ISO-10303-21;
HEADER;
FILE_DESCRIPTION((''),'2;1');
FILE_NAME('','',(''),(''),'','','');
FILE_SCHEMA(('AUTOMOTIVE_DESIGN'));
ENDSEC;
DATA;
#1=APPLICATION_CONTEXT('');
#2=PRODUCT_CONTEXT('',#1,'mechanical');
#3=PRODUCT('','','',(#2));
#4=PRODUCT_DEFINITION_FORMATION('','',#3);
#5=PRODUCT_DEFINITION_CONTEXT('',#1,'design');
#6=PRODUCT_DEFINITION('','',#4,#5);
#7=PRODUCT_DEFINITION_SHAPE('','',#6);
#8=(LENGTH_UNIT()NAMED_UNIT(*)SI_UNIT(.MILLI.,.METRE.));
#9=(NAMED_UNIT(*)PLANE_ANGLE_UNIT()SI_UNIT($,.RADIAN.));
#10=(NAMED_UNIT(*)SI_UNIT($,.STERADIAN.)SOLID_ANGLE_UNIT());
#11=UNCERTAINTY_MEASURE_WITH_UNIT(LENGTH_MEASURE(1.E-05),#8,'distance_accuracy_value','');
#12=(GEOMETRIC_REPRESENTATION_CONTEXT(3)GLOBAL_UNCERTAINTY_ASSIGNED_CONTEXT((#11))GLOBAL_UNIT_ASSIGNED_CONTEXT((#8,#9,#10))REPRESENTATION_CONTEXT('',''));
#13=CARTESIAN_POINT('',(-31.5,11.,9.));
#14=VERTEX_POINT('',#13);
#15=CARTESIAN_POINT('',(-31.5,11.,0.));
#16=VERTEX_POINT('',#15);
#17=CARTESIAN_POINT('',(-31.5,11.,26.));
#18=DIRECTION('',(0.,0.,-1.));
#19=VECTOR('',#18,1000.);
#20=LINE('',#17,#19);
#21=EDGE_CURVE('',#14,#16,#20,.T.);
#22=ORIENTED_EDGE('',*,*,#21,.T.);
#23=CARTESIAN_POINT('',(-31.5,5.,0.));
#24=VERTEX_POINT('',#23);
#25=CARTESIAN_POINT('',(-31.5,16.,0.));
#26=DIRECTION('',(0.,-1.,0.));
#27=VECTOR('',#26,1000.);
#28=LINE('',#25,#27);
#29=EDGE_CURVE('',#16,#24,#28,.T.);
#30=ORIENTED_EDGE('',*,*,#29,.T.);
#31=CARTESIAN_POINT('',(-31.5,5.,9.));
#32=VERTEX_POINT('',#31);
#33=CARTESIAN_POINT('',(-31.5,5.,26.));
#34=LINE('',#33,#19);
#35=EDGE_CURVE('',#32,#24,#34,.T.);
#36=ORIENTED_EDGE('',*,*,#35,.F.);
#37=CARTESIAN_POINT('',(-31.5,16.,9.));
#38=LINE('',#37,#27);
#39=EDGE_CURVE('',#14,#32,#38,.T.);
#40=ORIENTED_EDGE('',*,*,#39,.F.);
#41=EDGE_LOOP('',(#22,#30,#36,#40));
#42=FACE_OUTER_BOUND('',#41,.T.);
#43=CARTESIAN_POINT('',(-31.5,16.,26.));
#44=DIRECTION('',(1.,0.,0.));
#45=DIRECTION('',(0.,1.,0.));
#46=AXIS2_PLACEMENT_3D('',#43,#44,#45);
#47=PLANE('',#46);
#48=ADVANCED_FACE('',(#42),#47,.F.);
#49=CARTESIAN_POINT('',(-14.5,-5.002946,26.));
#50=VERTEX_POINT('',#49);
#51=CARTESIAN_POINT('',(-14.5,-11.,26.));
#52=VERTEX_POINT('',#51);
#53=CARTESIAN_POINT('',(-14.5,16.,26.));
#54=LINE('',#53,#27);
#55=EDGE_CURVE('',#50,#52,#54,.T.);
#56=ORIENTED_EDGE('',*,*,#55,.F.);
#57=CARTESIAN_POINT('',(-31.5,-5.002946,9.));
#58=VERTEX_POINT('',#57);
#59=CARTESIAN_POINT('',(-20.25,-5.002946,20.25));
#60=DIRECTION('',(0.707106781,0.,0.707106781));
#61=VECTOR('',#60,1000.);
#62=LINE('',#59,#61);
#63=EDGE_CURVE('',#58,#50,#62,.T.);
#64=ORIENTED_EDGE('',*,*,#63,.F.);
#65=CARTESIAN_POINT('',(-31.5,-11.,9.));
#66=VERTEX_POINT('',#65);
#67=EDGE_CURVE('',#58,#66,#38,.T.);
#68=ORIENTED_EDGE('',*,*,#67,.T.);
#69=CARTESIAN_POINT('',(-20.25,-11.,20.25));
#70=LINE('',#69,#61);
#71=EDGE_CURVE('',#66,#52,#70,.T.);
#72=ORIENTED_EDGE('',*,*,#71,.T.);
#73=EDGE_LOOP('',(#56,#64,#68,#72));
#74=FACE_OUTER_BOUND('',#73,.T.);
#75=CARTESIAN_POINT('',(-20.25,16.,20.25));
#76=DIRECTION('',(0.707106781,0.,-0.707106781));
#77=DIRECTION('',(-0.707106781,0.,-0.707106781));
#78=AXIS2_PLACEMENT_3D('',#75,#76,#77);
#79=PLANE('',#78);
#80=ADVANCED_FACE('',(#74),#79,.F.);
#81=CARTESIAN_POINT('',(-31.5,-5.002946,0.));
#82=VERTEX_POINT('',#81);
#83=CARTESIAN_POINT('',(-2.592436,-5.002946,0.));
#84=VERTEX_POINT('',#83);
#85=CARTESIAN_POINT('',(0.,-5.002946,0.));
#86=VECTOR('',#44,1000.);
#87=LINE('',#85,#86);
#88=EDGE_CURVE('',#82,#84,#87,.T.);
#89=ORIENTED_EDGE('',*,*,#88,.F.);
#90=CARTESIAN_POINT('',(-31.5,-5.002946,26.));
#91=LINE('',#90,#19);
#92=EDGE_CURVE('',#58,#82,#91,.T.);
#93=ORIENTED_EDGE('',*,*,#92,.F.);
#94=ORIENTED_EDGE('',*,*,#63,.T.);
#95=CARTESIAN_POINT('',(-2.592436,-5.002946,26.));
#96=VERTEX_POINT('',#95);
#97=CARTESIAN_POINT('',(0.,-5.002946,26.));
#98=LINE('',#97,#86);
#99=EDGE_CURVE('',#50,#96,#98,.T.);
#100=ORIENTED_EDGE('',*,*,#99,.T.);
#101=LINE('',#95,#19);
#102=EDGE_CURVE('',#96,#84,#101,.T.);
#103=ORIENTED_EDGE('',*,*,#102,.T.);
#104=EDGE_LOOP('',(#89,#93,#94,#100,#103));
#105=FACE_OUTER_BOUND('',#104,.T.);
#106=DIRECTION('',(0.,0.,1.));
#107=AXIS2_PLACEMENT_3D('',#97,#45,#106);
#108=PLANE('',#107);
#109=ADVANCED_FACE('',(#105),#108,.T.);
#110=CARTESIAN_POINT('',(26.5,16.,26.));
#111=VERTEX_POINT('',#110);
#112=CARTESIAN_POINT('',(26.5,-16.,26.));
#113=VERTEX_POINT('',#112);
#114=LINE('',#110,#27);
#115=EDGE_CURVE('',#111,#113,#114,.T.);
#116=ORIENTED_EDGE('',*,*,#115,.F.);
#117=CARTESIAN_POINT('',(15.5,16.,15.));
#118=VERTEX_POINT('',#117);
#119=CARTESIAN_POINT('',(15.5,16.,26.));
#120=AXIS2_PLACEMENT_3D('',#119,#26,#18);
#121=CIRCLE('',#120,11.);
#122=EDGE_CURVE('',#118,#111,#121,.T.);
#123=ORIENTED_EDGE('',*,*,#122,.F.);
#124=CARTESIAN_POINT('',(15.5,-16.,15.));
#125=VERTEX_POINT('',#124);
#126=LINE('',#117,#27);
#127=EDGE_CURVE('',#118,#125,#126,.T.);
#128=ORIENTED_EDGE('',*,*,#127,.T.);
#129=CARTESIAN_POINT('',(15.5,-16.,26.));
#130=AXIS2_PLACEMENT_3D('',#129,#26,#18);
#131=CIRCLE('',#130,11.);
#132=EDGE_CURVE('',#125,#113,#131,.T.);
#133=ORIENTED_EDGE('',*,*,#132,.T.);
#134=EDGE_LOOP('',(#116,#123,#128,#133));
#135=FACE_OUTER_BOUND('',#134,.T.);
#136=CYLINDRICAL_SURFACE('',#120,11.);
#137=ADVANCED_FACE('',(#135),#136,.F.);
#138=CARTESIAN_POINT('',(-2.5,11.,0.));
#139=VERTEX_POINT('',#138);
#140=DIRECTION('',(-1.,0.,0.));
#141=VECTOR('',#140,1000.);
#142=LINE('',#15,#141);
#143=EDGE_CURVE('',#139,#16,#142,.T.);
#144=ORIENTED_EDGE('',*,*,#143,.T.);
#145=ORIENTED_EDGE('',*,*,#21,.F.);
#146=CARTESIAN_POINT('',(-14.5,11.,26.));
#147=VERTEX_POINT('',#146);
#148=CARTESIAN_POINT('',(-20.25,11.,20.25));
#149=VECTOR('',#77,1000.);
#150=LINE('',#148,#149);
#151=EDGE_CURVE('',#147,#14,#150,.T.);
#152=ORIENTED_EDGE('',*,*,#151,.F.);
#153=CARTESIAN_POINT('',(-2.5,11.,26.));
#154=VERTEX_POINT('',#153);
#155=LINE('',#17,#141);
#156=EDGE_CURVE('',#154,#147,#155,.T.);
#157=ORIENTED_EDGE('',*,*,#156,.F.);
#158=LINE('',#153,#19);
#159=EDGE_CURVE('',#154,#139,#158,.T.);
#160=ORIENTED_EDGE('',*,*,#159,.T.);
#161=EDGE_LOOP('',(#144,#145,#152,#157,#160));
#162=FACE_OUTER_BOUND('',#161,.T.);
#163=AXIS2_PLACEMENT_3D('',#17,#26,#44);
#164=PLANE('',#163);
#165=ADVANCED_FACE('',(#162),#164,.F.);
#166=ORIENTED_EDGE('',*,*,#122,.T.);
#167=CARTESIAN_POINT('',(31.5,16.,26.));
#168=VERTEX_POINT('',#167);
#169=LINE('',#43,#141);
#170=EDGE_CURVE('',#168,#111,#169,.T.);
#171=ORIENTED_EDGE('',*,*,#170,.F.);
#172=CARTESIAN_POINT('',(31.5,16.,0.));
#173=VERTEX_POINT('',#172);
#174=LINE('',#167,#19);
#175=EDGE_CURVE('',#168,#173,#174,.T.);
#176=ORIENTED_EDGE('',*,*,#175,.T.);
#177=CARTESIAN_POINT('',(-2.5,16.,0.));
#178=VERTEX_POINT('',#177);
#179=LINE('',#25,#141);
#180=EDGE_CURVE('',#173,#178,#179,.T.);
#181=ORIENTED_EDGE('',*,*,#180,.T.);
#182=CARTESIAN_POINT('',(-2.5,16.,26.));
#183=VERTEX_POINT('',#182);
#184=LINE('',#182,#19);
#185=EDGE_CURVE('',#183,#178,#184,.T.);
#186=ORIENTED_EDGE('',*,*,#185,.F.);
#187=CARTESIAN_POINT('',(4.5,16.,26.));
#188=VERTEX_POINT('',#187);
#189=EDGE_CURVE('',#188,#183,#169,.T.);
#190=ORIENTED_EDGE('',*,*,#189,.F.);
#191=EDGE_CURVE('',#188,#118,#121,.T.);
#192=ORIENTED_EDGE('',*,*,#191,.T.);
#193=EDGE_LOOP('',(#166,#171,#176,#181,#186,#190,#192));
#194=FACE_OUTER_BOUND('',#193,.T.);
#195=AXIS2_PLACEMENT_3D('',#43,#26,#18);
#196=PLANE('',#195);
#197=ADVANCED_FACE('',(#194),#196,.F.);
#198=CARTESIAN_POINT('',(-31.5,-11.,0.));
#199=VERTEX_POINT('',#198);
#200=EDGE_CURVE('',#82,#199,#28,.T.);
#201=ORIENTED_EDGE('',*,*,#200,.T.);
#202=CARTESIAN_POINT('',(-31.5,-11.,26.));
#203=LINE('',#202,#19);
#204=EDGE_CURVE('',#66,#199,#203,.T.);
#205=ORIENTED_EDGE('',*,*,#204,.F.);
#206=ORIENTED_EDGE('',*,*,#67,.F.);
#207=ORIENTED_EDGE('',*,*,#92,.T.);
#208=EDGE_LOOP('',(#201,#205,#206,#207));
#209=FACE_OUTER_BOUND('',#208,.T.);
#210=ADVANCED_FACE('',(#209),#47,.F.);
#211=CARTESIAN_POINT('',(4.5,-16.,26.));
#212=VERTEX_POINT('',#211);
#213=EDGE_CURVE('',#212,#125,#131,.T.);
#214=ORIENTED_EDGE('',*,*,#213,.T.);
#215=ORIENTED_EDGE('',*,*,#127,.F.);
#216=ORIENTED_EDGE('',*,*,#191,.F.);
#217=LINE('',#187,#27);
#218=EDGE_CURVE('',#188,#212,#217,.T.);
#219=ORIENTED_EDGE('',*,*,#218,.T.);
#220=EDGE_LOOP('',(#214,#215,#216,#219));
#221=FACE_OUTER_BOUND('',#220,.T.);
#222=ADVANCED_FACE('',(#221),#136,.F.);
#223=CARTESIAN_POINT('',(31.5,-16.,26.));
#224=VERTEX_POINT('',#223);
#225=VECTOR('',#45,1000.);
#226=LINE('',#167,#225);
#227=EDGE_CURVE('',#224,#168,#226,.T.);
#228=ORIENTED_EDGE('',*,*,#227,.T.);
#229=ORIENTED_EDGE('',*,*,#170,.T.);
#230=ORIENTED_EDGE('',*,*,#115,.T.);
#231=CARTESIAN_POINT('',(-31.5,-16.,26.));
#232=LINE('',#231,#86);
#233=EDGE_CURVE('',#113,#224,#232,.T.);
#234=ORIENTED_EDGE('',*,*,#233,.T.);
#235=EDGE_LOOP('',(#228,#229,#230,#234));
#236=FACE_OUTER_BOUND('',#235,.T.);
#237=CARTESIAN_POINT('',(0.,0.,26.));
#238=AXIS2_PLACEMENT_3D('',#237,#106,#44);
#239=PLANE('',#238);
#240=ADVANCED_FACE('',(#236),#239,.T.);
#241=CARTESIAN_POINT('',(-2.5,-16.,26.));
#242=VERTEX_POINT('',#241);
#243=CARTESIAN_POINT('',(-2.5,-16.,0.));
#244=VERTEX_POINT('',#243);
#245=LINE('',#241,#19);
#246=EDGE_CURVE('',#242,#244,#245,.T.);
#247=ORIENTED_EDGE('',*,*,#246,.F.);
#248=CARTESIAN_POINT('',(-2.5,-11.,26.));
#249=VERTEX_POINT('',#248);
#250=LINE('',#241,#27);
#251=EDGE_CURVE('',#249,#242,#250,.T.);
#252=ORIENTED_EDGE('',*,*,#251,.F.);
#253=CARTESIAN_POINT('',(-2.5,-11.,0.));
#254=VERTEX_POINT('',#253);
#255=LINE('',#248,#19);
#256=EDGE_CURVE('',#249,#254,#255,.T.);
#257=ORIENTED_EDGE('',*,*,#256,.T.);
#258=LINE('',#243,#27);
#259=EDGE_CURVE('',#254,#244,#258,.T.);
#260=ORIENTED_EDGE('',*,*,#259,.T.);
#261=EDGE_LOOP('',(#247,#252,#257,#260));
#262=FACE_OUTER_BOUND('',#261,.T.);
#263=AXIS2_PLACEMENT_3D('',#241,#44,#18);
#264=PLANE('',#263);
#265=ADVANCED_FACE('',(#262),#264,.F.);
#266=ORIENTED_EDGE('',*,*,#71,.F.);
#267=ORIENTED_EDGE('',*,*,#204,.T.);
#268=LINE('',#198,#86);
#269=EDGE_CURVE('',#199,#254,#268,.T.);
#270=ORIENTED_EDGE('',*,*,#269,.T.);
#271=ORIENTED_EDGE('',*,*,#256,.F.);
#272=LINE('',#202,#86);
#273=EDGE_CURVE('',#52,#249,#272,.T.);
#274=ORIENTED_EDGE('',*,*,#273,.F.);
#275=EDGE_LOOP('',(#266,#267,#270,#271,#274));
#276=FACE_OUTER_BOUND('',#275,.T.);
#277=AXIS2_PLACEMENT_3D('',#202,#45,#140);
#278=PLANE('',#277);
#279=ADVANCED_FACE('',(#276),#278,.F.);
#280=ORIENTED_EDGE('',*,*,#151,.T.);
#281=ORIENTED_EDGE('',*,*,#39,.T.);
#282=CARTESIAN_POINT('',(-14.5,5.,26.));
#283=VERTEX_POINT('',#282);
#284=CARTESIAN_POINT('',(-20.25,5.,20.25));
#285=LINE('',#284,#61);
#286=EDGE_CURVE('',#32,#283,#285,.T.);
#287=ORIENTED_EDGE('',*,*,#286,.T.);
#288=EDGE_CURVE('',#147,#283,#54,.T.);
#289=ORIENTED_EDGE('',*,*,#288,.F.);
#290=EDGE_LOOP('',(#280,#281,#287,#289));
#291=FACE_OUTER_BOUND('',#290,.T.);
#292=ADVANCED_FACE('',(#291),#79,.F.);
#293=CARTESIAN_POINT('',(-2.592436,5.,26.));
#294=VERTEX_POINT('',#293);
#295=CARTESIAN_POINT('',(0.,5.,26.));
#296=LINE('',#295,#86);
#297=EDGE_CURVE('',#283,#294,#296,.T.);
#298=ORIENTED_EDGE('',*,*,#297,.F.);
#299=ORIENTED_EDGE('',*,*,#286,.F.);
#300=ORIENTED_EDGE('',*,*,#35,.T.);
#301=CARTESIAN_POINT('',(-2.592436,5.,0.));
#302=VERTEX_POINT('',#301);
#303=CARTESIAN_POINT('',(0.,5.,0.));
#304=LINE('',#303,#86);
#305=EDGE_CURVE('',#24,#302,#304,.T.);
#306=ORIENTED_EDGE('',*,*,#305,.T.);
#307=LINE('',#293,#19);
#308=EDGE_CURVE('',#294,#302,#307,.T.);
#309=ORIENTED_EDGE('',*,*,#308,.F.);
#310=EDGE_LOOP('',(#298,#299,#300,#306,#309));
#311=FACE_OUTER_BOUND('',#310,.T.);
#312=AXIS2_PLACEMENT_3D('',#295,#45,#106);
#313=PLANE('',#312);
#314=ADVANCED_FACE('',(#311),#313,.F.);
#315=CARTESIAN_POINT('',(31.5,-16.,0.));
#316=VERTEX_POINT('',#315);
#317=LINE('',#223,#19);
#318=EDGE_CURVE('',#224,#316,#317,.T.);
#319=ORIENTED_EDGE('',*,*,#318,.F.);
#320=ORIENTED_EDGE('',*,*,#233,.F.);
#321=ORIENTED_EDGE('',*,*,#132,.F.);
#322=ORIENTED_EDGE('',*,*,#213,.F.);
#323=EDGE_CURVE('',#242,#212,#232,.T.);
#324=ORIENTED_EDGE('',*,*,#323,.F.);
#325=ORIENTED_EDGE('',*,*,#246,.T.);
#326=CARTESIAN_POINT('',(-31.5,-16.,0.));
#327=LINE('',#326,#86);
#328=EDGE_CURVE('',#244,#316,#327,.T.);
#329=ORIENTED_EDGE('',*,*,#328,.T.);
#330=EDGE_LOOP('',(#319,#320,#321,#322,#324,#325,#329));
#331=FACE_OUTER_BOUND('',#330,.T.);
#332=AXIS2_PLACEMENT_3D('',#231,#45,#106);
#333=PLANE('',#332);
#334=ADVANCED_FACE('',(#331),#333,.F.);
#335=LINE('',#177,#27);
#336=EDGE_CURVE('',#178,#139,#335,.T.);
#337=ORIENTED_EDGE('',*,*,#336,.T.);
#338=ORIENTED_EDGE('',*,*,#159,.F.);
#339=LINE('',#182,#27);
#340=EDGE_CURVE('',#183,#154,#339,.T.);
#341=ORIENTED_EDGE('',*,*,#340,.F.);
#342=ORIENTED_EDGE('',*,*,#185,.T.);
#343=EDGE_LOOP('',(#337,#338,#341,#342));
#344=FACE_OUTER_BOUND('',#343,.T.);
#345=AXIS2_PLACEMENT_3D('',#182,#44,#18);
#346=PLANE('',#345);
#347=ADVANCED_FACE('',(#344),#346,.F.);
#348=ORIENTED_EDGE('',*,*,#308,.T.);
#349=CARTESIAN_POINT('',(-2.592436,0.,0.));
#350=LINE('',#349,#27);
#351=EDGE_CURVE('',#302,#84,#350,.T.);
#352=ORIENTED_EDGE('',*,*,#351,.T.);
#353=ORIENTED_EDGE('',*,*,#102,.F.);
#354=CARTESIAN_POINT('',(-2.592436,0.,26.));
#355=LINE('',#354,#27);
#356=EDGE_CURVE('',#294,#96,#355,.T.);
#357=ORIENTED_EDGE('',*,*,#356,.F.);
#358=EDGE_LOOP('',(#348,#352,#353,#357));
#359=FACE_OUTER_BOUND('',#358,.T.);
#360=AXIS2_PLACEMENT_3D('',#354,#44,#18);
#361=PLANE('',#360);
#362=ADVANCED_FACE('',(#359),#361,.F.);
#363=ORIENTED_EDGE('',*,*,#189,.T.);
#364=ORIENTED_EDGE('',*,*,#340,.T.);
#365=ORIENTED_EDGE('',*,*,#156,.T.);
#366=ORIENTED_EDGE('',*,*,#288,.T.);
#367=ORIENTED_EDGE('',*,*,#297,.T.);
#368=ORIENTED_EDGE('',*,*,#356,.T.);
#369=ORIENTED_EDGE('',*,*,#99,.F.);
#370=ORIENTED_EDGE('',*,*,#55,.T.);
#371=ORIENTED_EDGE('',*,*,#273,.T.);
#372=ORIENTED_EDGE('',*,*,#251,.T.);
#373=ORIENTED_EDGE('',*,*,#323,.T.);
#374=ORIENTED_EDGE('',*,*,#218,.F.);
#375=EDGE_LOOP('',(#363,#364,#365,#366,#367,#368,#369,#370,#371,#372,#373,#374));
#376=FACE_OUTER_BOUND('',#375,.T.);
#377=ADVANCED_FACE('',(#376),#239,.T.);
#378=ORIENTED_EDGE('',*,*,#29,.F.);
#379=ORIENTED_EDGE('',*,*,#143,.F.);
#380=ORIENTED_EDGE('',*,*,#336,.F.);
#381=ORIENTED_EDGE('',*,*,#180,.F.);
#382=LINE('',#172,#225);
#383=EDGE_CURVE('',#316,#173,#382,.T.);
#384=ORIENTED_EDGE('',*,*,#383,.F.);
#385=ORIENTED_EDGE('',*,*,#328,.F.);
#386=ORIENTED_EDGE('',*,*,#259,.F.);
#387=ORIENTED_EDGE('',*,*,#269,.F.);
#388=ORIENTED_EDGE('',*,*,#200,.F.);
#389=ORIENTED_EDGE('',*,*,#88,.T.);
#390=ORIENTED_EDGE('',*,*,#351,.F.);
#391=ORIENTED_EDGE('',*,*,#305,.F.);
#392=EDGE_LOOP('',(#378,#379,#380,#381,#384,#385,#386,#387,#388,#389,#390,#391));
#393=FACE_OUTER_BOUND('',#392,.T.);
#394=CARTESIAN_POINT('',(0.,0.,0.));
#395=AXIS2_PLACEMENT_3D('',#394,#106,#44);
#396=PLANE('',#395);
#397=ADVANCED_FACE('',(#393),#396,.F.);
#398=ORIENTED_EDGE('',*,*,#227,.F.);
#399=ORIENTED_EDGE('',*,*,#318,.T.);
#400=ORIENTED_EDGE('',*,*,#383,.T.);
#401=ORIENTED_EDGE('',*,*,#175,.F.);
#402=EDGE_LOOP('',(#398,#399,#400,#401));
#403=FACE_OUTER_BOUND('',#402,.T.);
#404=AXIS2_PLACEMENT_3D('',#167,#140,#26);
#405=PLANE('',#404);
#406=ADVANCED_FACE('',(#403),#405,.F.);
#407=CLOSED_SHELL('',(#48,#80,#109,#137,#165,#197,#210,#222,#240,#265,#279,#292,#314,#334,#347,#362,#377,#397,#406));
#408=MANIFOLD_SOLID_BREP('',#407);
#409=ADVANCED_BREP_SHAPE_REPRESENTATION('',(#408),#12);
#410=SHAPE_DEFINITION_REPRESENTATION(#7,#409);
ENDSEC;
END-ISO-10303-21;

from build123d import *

# Parameters (mm, degrees)
BASE_BLOCK_PROFILE_63X32_W  = 63
BASE_BLOCK_PROFILE_63X32_H  = 32
BASE_BLOCK_63X32X26_DEPTH   = 26
BORE_SLOT_CUT_DEPTH         = 32
RECTANGULAR_SLOT_17X9_DEPTH = 32
SIDE_STEP_PROFILE_W         = 29
SIDE_STEP_PROFILE_H         = 5
SIDE_STEP_CUT_DEPTH         = 44.866274061
SIDE_GROOVE_CUT_DEPTH       = 44.866274061


with BuildPart() as part:
    # Base Block Profile 63x32 → Base Block 63x32x26 (new body)
    with BuildSketch(Plane.XY):
        Rectangle(BASE_BLOCK_PROFILE_63X32_W, BASE_BLOCK_PROFILE_63X32_H)
    extrude(amount=BASE_BLOCK_63X32X26_DEPTH)

    # Bore Slot Profile → Bore Slot Cut (cut)
    with BuildSketch(Plane.XZ.offset(16)):
        with BuildLine():
            ThreePointArc((4.5, 26), (15.5, 15), (26.5, 26))
            Line((26.5, 26), (4.5, 26))
        make_face()
    extrude(amount=-BORE_SLOT_CUT_DEPTH, mode=Mode.SUBTRACT)

    # Rectangular Slot Profile 17x9 → Rectangular Slot 17x9 (cut)
    with BuildSketch(Plane(origin=(0, -16, 0), x_dir=(-1, 0, 0), z_dir=(0, -1, 0))):
        Polygon((31.5, -9), (14.5, -26), (31.5, -26), align=None)
    extrude(amount=-RECTANGULAR_SLOT_17X9_DEPTH, mode=Mode.SUBTRACT)

    # Side Step Profile → Side Step Cut (cut, through all)
    with BuildSketch(Plane(origin=(0, 0, 0), x_dir=(-1, 0, 0), z_dir=(0, 0, -1))):
        with Locations((17, 13.5)):
            Rectangle(SIDE_STEP_PROFILE_W, SIDE_STEP_PROFILE_H)
        with Locations((17, -13.5)):
            Rectangle(SIDE_STEP_PROFILE_W, SIDE_STEP_PROFILE_H)
    extrude(amount=-SIDE_STEP_CUT_DEPTH, mode=Mode.SUBTRACT)

    # Side Groove Profile → Side Groove Cut (cut, through all)
    with BuildSketch(Plane(origin=(0, 0, 0), x_dir=(-1, 0, 0), z_dir=(0, 0, -1))):
        Polygon((31.5, -5.002946395), (31.5, 0), (31.5, 5), (2.592435859, 5), (2.592435859, -5.002946395), align=None)
    extrude(amount=-SIDE_GROOVE_CUT_DEPTH, mode=Mode.SUBTRACT)


solid = part.part
